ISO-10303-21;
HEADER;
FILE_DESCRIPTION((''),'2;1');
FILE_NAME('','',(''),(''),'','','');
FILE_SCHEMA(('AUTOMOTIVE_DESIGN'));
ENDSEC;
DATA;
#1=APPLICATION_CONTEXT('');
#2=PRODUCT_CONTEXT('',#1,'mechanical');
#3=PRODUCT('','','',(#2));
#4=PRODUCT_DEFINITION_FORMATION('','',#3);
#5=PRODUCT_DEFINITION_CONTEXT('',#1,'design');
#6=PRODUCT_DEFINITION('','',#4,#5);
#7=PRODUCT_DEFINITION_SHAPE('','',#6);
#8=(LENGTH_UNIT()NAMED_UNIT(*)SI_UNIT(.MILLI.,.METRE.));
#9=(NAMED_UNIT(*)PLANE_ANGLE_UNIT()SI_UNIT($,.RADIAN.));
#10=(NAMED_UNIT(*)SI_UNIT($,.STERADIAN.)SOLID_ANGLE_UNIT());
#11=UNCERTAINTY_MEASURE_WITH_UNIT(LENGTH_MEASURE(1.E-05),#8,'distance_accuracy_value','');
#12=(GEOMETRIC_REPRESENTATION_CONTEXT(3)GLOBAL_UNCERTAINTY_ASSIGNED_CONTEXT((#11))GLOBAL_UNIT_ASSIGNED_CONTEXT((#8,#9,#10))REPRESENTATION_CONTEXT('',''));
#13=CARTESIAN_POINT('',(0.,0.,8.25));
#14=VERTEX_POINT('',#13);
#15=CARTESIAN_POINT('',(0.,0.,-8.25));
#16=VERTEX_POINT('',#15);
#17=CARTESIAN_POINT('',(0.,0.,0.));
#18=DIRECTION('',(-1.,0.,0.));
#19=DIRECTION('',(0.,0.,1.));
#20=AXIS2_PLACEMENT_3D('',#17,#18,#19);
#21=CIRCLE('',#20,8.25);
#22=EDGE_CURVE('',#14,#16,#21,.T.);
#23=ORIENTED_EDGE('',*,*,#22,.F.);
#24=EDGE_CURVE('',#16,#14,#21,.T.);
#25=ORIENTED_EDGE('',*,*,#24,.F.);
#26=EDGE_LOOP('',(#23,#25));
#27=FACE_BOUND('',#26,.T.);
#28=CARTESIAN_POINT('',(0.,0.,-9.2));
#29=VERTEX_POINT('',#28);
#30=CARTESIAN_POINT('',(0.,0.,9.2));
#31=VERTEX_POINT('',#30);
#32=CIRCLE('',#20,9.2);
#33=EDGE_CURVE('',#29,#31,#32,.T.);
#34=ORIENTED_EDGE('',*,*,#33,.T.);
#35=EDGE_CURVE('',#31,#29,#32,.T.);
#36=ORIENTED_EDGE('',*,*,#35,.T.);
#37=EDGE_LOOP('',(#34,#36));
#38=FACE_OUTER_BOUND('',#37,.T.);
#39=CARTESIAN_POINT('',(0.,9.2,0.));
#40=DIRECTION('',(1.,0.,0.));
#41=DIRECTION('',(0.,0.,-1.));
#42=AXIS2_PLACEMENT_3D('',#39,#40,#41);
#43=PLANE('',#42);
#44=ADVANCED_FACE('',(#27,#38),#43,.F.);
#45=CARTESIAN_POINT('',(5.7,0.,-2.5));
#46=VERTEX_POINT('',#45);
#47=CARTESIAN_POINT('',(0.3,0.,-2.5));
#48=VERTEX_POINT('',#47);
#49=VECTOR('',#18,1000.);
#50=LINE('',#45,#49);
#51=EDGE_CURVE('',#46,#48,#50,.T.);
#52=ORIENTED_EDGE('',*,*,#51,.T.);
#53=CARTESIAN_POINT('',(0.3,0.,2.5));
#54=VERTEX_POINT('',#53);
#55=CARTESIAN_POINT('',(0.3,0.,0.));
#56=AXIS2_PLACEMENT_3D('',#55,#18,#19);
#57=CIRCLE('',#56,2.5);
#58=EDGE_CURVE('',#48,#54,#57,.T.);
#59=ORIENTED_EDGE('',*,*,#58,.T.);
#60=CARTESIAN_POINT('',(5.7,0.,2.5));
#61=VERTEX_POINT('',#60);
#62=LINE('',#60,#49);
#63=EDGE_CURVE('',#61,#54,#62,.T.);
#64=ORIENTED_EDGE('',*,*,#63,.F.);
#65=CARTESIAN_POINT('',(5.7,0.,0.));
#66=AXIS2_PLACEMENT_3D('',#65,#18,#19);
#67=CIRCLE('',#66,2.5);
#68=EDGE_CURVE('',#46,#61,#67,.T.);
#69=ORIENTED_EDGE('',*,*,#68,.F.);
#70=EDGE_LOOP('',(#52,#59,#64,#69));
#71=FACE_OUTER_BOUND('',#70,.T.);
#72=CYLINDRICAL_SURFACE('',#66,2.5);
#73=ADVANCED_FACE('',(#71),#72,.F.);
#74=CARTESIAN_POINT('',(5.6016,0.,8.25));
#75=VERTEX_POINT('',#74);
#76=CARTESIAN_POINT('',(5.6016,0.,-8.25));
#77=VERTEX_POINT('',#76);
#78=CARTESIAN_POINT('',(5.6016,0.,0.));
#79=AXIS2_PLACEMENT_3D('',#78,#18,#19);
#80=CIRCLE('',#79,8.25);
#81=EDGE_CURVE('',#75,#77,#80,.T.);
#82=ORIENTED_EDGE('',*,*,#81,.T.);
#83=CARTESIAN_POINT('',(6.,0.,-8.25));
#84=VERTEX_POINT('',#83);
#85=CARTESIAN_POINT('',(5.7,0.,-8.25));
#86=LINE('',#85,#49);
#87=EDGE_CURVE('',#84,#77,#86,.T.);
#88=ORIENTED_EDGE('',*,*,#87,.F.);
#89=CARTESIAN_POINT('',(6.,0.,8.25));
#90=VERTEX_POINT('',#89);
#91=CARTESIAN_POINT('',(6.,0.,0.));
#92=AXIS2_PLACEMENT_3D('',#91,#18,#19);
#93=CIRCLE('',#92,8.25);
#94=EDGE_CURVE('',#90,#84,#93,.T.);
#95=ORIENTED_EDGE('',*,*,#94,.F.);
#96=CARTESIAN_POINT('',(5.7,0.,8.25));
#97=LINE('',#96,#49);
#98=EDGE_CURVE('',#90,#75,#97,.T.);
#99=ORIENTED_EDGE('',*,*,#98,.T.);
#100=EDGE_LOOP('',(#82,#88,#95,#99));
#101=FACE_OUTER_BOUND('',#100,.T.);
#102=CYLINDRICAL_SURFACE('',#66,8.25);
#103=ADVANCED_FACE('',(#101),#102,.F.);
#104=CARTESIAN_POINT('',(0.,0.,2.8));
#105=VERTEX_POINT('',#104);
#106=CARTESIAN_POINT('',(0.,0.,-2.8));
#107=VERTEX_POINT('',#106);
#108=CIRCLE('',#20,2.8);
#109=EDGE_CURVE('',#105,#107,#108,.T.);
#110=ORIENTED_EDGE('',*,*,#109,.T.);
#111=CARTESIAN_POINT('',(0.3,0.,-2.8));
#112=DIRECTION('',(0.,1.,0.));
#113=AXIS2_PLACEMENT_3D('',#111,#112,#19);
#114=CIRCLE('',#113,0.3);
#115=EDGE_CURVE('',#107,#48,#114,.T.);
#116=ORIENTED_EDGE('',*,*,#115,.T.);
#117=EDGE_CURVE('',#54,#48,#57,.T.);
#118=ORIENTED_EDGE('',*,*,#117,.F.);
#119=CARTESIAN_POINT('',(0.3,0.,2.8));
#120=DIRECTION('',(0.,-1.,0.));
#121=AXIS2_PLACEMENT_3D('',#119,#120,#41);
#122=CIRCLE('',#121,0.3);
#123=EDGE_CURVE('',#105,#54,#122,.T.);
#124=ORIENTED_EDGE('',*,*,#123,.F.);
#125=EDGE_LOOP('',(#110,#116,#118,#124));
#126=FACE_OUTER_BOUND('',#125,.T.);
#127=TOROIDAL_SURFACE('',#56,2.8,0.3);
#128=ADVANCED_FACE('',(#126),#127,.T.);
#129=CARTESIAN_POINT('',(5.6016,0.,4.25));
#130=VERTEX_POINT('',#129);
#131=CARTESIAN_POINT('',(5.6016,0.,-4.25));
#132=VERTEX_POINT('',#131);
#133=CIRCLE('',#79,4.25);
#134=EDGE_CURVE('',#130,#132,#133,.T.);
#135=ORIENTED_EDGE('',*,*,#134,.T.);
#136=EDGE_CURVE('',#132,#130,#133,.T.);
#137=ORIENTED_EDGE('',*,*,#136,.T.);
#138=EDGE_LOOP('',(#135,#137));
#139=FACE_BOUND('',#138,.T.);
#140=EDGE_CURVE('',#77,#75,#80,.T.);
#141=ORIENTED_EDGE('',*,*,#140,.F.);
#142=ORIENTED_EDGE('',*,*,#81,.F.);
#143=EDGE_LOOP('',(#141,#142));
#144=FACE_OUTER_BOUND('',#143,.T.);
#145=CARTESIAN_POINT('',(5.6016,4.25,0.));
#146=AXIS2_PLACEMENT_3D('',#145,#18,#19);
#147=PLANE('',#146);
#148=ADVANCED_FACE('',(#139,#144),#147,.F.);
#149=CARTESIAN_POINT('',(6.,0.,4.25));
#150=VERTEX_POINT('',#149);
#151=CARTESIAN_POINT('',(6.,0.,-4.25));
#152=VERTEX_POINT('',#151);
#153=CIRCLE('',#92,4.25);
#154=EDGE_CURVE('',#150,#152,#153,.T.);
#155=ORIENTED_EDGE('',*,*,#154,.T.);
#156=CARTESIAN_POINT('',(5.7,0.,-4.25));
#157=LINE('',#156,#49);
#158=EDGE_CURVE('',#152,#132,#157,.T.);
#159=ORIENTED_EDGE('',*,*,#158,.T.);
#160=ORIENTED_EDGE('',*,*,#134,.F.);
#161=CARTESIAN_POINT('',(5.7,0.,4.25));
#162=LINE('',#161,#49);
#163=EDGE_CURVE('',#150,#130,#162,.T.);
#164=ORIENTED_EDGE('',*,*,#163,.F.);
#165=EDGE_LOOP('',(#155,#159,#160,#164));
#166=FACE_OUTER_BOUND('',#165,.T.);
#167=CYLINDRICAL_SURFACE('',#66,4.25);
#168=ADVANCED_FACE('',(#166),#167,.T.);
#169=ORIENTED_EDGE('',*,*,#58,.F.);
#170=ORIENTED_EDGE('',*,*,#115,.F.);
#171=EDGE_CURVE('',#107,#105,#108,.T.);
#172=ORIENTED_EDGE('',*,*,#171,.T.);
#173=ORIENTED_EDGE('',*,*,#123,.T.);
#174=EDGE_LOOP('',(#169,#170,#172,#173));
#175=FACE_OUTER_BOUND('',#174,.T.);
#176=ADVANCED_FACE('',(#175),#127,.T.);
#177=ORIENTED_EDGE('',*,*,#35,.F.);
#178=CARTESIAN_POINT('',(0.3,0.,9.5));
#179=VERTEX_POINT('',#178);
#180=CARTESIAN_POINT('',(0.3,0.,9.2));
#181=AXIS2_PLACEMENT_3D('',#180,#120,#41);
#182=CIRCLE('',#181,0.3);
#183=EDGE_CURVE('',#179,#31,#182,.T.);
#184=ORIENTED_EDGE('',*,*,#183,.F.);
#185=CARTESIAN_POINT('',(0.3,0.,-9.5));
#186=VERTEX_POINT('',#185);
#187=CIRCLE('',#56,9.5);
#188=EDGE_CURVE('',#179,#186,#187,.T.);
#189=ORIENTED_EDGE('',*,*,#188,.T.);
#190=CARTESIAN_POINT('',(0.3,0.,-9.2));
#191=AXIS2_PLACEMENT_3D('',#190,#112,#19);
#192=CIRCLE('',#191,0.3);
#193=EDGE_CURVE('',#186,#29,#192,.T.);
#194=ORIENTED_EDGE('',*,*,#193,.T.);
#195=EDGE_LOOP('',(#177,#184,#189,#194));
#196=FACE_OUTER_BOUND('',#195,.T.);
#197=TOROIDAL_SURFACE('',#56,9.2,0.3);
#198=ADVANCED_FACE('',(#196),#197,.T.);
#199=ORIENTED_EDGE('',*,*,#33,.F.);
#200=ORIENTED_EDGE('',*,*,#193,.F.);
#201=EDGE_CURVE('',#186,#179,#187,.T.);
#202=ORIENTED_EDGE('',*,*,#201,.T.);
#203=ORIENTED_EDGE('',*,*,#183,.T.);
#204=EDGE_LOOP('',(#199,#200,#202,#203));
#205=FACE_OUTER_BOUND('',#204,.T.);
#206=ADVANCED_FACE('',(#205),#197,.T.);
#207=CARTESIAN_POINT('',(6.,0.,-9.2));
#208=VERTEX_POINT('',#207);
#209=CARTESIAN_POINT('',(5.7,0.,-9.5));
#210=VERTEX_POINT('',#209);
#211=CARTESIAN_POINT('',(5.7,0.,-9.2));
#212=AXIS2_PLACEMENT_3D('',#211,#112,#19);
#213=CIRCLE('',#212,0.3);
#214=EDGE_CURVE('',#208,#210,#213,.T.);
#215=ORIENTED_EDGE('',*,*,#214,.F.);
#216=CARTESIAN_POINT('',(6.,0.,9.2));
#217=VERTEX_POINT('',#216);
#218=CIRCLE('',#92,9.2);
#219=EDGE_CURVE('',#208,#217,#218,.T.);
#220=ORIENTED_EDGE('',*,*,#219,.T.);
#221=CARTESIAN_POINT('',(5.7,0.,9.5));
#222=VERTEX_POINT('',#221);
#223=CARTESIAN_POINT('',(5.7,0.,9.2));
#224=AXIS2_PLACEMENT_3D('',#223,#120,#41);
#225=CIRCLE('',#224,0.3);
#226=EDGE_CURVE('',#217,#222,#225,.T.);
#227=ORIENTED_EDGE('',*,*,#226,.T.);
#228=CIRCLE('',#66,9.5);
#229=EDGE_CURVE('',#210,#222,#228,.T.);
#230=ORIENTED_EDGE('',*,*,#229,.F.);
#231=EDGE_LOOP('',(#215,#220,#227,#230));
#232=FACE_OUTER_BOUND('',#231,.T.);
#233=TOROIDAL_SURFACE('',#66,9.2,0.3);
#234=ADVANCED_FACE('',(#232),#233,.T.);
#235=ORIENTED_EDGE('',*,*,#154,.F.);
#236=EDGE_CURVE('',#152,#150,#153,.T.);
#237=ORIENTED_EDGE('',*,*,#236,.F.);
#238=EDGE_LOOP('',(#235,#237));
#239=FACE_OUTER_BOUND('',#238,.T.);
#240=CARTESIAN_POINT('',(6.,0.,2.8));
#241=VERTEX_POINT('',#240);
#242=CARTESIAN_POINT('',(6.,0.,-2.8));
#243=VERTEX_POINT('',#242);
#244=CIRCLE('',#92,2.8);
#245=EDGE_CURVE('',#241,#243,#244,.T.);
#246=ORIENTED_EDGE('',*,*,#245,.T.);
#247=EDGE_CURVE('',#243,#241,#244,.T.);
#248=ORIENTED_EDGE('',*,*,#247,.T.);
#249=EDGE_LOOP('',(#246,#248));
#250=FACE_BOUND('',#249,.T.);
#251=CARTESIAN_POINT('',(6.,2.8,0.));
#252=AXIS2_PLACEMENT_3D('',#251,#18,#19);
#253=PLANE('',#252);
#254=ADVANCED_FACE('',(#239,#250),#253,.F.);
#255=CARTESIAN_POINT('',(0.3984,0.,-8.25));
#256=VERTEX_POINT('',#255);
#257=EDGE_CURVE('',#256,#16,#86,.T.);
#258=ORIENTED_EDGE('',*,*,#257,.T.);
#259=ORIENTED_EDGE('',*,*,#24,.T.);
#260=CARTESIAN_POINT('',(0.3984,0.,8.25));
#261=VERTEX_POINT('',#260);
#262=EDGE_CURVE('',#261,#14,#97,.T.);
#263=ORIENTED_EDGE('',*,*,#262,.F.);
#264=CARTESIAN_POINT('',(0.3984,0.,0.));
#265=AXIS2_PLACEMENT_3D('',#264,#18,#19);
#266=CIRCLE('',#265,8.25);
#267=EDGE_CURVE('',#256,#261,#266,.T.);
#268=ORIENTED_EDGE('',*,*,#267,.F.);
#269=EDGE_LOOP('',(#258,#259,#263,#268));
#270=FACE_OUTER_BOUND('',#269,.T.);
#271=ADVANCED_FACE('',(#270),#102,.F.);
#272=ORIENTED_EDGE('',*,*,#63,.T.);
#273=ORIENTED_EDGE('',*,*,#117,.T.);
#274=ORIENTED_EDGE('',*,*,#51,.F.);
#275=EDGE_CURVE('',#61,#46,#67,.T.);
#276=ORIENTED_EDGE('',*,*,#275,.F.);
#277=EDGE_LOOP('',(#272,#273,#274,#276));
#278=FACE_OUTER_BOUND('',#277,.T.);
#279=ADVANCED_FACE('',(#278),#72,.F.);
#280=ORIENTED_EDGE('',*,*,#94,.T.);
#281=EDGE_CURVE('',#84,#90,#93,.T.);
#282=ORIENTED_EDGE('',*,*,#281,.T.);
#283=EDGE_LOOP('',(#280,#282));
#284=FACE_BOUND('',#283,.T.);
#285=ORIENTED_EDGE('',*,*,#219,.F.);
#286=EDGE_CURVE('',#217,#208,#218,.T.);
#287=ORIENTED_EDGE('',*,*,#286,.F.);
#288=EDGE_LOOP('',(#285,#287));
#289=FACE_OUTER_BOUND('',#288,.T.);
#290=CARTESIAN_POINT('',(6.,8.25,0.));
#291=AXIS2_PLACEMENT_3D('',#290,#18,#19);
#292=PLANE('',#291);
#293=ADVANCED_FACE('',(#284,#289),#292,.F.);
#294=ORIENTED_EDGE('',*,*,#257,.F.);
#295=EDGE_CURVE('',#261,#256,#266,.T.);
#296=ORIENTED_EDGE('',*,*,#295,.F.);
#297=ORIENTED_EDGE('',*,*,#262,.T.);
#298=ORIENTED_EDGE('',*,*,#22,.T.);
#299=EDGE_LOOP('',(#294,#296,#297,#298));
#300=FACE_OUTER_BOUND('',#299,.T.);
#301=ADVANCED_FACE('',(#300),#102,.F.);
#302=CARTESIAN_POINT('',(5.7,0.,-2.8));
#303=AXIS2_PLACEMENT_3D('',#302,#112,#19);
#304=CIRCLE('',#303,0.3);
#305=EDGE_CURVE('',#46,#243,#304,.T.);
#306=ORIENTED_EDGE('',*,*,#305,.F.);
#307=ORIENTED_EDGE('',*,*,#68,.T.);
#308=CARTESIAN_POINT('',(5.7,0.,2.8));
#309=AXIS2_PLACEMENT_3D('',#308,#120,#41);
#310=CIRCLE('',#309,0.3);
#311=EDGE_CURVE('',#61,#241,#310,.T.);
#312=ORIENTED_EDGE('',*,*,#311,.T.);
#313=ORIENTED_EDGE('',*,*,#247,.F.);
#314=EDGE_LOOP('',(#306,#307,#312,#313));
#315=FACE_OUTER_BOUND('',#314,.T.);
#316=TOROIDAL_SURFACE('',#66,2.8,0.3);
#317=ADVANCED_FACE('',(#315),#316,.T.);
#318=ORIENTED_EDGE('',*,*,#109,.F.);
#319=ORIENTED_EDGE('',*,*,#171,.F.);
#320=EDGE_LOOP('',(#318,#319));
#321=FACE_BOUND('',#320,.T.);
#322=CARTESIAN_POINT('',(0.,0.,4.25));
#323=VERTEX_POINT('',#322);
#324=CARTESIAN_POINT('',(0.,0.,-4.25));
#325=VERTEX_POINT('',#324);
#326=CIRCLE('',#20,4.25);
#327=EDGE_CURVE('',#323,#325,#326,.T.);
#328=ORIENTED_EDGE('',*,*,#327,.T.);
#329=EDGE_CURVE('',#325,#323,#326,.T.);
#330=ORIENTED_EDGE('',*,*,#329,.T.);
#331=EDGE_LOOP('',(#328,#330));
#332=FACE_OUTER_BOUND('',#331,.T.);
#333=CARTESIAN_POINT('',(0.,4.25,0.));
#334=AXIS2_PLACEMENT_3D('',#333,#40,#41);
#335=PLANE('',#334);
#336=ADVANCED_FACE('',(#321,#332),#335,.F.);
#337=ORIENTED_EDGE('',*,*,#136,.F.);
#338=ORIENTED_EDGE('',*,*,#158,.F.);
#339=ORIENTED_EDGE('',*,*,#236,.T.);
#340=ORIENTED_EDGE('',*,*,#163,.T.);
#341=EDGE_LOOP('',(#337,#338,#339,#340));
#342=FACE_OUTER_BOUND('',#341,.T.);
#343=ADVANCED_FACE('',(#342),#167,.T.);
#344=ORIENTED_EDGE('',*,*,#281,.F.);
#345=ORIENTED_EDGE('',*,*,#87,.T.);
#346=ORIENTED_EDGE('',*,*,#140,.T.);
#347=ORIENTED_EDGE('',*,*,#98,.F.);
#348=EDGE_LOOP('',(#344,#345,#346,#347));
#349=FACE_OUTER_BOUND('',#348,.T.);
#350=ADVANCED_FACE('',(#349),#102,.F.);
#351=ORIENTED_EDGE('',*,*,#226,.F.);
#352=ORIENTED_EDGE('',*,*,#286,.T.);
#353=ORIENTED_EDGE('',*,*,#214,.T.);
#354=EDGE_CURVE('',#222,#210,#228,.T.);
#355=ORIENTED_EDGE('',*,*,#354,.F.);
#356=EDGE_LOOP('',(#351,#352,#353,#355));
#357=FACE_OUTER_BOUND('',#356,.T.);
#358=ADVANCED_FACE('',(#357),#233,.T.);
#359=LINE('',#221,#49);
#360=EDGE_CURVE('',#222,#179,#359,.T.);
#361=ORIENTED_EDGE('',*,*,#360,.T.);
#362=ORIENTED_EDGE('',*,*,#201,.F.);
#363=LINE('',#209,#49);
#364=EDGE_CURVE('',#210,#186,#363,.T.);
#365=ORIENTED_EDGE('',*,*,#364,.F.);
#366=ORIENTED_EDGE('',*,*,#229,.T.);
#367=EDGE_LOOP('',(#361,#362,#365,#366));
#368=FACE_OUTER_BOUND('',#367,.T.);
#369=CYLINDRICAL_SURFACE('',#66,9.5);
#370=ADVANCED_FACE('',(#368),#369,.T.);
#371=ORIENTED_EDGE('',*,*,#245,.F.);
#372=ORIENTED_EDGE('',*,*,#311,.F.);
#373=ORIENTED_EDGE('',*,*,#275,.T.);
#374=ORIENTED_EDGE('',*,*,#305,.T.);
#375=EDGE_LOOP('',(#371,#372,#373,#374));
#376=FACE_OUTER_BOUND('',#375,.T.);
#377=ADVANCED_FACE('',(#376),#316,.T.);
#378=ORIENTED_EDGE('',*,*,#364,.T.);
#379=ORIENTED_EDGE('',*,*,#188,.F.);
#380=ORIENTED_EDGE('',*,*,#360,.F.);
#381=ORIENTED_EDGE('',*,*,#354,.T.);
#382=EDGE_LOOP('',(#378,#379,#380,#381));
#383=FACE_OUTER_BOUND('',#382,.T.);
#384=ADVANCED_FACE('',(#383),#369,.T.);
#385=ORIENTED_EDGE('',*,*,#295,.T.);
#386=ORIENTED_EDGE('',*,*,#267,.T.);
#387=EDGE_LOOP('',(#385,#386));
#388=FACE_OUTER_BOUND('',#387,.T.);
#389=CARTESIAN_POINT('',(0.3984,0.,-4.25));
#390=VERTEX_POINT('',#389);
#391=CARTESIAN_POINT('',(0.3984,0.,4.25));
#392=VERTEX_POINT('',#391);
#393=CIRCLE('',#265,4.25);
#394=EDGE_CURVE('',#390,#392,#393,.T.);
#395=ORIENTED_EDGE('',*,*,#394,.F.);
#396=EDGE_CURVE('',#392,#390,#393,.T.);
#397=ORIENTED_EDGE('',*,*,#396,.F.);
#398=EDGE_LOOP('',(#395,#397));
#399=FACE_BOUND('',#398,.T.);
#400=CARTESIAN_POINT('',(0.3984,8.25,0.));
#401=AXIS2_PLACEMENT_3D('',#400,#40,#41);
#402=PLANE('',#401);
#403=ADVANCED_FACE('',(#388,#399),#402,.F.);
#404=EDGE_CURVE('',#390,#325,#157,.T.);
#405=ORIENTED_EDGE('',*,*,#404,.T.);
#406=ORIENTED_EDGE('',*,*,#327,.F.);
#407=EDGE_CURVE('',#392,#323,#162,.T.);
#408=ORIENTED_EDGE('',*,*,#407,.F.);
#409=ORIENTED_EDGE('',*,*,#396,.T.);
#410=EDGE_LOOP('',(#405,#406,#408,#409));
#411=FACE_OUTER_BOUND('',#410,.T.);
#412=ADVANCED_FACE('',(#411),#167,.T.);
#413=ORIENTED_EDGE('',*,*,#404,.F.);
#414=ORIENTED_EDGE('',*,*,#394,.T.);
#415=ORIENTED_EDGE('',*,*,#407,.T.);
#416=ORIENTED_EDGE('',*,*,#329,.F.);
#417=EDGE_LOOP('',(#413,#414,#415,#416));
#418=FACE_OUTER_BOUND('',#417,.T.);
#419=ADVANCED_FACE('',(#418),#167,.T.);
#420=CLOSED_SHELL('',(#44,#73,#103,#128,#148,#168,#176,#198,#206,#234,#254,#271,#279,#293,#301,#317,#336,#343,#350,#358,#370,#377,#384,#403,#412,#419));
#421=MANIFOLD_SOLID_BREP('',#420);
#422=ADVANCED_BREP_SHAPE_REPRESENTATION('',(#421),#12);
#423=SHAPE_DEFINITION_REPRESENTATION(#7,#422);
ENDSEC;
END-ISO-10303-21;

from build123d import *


with BuildPart() as part:
    # 草图1 → 旋转1 (revolve)
    with BuildSketch(Plane.XY, mode=Mode.PRIVATE) as revolve_1_sk:
        with BuildLine():
            Line((0, 9.2), (0, 8.25))
            Line((0, 8.25), (0.3984, 8.25))
            Line((0.3984, 8.25), (0.3984, 4.25))
            Line((0.3984, 4.25), (0, 4.25))
            Line((0, 4.25), (0, 2.8))
            ThreePointArc((0, 2.8), (0.087867966, 2.587867966), (0.3, 2.5))
            Line((0.3, 2.5), (5.7, 2.5))
            ThreePointArc((5.7, 2.5), (5.912132034, 2.587867966), (6, 2.8))
            Line((6, 2.8), (6, 4.25))
            Line((6, 4.25), (5.6016, 4.25))
            Line((5.6016, 4.25), (5.6016, 8.25))
            Line((5.6016, 8.25), (6, 8.25))
            Line((6, 8.25), (6, 9.2))
            ThreePointArc((6, 9.2), (5.912132034, 9.412132034), (5.7, 9.5))
            Line((5.7, 9.5), (0.3, 9.5))
            ThreePointArc((0.3, 9.5), (0.087867966, 9.412132034), (0, 9.2))
        make_face()
    revolve(revolve_1_sk.sketch.rotate(Axis((5.7, 0, 0), (-1, 0, 0)), 270), axis=Axis((5.7, 0, 0), (-1, 0, 0)))


solid = part.part
